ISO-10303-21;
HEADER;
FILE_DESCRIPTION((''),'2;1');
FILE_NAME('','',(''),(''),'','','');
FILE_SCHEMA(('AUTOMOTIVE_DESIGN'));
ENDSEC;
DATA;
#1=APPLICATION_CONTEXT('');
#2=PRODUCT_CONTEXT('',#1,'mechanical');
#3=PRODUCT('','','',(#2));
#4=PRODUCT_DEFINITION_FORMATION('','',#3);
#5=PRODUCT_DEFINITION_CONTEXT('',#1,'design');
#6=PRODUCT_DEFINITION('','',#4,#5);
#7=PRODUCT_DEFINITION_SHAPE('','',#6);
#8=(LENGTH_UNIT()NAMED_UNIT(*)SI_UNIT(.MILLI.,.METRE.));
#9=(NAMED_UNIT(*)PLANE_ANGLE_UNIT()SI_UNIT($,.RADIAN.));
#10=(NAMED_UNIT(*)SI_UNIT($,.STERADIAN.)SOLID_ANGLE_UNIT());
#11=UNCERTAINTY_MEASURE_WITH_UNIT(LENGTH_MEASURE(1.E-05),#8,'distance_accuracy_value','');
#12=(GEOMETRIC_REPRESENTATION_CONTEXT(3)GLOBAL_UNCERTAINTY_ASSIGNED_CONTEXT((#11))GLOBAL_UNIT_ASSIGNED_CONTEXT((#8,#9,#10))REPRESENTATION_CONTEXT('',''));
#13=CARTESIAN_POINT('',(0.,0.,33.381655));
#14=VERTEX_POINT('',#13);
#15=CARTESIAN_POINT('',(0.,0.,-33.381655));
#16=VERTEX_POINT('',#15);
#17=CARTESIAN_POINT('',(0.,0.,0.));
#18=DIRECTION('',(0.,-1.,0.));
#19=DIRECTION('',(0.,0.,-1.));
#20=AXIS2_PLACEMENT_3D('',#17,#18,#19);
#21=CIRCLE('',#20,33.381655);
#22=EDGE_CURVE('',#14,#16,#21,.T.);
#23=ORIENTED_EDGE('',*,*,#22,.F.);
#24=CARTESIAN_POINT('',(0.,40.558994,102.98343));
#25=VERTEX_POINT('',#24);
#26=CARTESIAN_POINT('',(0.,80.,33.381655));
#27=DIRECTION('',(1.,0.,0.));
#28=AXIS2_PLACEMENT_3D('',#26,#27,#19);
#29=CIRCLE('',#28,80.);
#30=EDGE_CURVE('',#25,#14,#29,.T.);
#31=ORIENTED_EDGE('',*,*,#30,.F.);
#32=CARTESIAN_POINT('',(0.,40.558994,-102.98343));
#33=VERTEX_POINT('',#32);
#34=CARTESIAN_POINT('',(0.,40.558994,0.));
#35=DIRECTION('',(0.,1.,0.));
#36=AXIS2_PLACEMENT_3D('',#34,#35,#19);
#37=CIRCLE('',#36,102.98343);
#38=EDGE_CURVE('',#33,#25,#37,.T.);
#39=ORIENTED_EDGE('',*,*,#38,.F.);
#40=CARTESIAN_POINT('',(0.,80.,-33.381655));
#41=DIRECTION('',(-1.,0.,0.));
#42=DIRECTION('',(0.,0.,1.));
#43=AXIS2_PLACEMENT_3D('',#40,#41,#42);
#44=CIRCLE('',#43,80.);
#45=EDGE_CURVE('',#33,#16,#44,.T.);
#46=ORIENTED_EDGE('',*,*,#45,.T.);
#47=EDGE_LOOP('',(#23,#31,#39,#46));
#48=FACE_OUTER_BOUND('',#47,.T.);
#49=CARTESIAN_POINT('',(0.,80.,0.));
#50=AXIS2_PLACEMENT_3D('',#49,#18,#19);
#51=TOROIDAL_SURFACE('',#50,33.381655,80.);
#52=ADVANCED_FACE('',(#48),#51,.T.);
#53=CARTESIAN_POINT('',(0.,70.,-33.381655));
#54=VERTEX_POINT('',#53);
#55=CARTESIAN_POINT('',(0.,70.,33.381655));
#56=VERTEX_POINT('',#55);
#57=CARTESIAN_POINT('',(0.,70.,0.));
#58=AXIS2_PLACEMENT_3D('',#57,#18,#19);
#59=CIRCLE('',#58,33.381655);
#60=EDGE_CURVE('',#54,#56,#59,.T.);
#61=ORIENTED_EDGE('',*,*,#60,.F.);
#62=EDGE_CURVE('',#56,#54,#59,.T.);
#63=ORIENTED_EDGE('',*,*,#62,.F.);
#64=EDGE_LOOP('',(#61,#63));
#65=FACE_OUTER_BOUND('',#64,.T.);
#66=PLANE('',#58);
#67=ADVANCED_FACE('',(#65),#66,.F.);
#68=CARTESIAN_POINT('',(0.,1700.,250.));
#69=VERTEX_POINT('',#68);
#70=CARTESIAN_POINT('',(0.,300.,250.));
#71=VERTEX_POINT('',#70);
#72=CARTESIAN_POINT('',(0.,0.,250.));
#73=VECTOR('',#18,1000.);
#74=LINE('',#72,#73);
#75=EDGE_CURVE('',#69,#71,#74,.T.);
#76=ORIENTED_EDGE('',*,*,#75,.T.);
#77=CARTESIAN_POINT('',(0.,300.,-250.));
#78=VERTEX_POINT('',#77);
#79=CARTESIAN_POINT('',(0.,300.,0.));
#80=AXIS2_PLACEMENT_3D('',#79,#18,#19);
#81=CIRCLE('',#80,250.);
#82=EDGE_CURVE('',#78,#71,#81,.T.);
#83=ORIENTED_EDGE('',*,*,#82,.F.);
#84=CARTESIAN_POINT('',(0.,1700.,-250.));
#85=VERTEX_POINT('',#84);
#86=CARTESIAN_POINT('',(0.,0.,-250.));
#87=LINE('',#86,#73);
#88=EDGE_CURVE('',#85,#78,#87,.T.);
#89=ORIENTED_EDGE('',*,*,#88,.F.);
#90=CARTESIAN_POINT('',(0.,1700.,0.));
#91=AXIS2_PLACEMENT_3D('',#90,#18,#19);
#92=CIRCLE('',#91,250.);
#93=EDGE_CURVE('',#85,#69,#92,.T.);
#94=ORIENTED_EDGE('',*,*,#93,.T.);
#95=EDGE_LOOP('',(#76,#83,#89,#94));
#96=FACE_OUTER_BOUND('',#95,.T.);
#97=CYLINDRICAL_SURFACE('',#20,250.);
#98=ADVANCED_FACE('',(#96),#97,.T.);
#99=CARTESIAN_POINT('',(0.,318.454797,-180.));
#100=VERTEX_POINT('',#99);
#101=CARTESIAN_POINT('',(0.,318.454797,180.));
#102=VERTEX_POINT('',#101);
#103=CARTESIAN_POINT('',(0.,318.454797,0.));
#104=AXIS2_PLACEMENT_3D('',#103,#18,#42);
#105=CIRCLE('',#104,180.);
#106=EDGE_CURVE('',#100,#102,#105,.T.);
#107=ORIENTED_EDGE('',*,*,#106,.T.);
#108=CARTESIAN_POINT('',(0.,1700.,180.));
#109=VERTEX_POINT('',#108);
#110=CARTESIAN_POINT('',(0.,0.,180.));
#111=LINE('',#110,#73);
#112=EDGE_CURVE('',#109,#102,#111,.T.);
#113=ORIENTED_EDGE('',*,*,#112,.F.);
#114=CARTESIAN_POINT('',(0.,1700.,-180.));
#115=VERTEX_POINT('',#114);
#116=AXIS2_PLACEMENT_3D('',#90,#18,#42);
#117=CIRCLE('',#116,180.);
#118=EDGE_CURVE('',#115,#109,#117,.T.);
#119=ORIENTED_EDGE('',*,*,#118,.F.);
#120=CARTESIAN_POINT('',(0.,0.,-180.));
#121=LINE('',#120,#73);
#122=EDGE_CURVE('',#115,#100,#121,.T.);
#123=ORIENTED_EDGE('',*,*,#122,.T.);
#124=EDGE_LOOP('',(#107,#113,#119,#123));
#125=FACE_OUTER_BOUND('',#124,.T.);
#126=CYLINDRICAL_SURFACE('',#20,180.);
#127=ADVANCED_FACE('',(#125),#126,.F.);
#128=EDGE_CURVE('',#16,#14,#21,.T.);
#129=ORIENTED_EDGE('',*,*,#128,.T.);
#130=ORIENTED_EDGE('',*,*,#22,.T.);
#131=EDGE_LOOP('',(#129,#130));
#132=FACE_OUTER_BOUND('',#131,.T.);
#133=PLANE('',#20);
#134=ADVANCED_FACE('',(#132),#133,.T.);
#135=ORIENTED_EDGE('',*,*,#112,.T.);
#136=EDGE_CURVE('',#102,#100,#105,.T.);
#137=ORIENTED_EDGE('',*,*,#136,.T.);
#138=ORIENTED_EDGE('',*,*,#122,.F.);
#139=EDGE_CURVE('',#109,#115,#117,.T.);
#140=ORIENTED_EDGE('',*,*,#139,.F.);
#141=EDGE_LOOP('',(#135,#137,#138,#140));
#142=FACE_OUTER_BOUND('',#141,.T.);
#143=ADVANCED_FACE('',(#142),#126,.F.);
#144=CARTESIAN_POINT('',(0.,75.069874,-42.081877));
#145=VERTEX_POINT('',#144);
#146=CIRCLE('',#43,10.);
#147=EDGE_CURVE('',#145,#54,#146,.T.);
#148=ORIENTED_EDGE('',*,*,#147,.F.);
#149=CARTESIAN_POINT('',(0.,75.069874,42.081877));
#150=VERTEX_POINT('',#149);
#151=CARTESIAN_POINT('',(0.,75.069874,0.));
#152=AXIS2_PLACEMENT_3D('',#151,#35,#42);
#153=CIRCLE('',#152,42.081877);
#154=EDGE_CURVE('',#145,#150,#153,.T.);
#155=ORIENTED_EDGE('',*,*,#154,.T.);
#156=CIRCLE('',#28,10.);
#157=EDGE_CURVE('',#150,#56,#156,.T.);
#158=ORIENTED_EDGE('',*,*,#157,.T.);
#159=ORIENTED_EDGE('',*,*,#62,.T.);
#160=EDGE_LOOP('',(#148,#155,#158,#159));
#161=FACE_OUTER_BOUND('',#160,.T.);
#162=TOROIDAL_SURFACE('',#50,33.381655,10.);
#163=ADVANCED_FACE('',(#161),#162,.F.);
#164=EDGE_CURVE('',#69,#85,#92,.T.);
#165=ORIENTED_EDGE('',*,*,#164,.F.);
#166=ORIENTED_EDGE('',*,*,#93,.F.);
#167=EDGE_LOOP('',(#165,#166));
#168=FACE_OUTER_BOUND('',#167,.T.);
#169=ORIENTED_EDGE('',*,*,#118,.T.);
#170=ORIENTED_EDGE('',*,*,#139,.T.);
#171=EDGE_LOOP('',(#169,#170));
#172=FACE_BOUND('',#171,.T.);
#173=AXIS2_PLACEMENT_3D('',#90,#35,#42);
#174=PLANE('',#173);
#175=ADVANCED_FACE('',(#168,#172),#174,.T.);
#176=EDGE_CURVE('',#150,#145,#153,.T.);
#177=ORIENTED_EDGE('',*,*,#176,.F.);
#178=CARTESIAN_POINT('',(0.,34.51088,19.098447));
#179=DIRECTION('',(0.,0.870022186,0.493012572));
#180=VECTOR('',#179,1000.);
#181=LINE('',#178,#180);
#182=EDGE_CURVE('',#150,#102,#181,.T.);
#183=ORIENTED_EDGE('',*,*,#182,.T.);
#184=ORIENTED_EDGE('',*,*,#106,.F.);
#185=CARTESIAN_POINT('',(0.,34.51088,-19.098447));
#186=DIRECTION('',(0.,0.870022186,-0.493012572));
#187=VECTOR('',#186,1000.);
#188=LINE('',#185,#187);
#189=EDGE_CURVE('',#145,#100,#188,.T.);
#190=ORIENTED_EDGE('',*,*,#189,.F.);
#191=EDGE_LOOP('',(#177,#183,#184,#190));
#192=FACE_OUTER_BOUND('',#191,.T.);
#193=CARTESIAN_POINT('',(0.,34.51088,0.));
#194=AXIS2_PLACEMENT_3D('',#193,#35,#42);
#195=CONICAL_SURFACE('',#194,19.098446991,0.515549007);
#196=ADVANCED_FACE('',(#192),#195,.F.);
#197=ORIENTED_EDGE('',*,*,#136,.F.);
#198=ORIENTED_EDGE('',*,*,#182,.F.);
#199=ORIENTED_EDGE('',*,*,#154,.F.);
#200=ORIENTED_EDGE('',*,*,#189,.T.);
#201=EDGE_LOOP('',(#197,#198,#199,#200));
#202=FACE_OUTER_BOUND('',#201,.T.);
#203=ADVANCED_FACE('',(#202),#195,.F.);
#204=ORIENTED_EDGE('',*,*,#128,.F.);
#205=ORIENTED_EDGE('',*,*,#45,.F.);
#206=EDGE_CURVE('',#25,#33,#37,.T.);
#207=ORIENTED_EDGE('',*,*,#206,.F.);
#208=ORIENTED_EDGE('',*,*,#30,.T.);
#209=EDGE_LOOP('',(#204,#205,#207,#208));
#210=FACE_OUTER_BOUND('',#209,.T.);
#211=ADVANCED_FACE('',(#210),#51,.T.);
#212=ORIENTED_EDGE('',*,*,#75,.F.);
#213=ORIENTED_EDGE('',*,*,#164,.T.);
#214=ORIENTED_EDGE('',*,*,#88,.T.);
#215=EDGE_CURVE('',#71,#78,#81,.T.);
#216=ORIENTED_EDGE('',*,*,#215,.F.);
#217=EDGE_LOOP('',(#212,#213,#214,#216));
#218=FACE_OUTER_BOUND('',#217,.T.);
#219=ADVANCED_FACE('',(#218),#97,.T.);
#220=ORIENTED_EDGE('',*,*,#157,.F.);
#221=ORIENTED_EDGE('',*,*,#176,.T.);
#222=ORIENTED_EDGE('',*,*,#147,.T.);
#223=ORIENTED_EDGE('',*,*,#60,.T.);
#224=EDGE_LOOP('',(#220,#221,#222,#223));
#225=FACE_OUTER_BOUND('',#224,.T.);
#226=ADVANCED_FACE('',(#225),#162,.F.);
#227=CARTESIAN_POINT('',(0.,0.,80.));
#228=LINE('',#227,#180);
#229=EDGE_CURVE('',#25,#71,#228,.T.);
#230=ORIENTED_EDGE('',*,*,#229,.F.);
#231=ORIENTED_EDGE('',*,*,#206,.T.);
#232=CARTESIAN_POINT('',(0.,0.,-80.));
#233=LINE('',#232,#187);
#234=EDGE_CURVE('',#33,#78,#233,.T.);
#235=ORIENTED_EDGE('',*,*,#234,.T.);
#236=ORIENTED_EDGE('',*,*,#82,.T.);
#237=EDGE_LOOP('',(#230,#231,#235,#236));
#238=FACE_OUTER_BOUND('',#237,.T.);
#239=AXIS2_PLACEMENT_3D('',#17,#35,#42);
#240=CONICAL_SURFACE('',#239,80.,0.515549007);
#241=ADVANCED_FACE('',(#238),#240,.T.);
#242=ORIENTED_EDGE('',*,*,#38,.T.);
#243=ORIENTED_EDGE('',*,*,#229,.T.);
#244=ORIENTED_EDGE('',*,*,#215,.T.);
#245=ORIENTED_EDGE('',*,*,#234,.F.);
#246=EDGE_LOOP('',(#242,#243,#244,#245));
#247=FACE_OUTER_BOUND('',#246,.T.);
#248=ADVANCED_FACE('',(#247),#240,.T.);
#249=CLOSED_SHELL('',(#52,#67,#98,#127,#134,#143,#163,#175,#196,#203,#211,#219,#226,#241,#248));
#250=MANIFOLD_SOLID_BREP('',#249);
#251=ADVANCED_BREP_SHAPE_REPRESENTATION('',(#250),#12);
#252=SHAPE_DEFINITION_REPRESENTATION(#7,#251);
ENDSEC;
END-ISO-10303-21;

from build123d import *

# Parameters (mm, degrees)
FILLET1_R = 80
SHELL1_T  = -70


with BuildPart() as part:
    # Sketch2 → Revolve1 (revolve)
    with BuildSketch(Plane.XY, mode=Mode.PRIVATE) as revolve1_sk:
        Polygon((0, 1700), (250, 1700), (250, 300), (80, 0), (0, 0), align=None)
    revolve(revolve1_sk.sketch.rotate(Axis((0, 0, 0), (0, 1, 0)), 270), axis=Axis((0, 0, 0), (0, 1, 0)))

    # Fillet1
    fillet1_edges = [part.edges().sort_by_distance(p)[0] for p in [
        (0, 0, -80),
    ]]
    fillet(fillet1_edges, radius=FILLET1_R)

    # Shell1
    shell1_openings = [part.faces().sort_by_distance(p)[0] for p in [
        (0, 1700, 0),
    ]]
    offset(amount=SHELL1_T, openings=shell1_openings, kind=Kind.INTERSECTION)


solid = part.part
